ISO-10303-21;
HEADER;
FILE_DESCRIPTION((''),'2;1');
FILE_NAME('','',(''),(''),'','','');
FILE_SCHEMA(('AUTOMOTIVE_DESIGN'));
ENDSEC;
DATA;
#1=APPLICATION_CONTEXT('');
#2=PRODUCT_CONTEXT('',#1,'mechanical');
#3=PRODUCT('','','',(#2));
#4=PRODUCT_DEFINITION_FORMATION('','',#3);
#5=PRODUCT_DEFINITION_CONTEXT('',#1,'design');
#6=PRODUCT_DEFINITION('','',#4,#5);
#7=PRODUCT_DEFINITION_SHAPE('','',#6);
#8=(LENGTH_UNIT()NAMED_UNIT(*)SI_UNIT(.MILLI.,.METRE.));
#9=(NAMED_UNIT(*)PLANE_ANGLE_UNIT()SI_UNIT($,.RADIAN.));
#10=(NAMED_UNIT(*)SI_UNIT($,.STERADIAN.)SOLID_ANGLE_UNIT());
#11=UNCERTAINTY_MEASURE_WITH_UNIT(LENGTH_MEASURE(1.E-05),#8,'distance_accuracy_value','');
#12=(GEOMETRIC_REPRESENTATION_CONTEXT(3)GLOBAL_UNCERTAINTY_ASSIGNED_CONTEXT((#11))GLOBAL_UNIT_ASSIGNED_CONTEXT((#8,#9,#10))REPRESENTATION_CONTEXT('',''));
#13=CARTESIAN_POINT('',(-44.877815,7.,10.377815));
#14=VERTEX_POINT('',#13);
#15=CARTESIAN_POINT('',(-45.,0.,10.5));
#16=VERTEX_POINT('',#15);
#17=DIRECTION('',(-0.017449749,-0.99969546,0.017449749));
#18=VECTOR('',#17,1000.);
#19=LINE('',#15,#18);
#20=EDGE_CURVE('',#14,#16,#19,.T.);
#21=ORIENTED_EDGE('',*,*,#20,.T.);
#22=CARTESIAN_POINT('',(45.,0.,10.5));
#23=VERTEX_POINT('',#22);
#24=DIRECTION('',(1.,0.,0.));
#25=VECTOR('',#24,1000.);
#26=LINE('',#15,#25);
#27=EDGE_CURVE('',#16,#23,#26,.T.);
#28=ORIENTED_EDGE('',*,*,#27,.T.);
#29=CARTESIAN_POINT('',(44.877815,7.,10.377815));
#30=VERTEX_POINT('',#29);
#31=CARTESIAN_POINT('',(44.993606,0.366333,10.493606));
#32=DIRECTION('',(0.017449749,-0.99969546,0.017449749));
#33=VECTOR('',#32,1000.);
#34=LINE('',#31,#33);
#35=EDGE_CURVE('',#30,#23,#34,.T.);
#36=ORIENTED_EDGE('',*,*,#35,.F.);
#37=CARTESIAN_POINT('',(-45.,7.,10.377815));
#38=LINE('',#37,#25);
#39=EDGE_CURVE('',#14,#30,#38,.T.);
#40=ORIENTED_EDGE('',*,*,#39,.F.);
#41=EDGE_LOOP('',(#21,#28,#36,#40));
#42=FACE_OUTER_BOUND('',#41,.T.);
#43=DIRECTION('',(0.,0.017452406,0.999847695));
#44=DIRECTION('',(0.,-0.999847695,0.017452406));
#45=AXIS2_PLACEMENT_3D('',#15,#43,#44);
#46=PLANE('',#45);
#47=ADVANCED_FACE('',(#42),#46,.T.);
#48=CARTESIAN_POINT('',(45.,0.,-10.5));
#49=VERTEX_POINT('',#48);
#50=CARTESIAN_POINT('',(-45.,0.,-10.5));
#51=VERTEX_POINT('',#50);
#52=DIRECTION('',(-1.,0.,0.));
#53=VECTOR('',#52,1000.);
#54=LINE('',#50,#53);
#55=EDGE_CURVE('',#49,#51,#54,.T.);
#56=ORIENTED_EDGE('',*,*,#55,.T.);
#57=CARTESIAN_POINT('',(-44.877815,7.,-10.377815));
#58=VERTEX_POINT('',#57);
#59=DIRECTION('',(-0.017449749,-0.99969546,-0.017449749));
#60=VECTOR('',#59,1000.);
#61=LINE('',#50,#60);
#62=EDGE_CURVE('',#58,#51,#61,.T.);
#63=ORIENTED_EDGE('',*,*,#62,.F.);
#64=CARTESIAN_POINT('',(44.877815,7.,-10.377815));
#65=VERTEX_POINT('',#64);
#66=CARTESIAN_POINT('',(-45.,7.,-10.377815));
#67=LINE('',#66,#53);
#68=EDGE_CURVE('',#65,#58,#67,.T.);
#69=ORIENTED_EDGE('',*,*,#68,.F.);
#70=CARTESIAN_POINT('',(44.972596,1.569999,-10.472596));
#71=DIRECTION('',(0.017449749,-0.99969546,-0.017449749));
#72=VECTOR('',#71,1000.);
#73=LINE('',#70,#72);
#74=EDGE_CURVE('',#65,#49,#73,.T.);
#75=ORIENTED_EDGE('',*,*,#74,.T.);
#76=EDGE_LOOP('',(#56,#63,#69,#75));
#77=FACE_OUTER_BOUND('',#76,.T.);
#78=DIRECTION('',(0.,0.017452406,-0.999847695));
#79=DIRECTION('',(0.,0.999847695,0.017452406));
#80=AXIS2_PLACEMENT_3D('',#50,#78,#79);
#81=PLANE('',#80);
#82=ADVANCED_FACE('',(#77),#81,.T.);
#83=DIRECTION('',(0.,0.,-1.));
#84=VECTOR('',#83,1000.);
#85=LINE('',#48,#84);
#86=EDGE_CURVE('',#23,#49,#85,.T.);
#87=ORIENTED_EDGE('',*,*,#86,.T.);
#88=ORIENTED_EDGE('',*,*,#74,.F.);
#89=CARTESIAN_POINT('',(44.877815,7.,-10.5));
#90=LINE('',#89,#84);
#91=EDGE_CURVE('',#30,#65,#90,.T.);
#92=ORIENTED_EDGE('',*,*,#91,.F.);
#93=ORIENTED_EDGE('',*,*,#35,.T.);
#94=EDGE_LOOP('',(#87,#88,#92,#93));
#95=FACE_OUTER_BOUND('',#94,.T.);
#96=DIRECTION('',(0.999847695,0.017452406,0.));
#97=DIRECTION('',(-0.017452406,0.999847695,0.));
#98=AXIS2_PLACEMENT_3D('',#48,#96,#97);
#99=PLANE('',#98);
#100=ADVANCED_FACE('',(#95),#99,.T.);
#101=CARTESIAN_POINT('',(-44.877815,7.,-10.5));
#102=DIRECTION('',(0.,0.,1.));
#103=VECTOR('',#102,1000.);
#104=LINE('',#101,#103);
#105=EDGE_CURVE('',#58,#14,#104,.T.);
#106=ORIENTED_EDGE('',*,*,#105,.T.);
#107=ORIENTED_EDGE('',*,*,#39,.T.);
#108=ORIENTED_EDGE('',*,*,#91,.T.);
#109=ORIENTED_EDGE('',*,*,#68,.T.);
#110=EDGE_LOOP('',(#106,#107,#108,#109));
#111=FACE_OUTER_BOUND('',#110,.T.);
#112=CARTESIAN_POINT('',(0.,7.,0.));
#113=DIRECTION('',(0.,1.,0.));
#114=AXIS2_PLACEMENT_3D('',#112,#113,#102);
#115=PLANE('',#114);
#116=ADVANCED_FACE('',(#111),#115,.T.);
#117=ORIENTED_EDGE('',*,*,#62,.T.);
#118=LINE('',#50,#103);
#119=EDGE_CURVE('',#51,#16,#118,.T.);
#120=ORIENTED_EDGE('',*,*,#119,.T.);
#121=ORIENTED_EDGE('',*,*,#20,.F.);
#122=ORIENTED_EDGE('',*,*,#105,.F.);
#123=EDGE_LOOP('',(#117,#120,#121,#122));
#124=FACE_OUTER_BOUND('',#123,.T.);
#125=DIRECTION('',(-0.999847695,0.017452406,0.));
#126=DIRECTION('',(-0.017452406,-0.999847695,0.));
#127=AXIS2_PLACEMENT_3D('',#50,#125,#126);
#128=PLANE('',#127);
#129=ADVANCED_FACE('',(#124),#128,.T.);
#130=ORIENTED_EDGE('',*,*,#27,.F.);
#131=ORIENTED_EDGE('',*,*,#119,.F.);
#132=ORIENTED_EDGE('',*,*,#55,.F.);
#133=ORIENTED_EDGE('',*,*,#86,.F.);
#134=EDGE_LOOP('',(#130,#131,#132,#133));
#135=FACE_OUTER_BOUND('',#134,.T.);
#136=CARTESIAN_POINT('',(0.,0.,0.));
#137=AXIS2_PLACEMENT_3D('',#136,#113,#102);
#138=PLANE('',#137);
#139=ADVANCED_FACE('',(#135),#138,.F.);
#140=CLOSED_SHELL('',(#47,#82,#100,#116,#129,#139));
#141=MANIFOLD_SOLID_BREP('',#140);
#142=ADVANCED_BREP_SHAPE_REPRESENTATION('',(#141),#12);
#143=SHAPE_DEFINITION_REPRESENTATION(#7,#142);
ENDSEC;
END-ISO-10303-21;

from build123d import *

# Parameters (mm, degrees)
COTTER_PROFILE_90X25_W          = 90
COTTER_PROFILE_90X25_H          = 21
COTTER_BODY_7MM_DRAFTED_1_DEPTH = 7
COTTER_BODY_7MM_DRAFTED_1_TAPER = 1


with BuildPart() as part:
    # Cotter Profile 90x25 → Cotter Body 7mm Drafted 1° (new body)
    with BuildSketch(Plane(origin=(0, 0, 0), x_dir=(1, 0, 0), z_dir=(0, 1, 0))):
        Rectangle(COTTER_PROFILE_90X25_W, COTTER_PROFILE_90X25_H)
    extrude(amount=COTTER_BODY_7MM_DRAFTED_1_DEPTH, taper=COTTER_BODY_7MM_DRAFTED_1_TAPER)


solid = part.part
